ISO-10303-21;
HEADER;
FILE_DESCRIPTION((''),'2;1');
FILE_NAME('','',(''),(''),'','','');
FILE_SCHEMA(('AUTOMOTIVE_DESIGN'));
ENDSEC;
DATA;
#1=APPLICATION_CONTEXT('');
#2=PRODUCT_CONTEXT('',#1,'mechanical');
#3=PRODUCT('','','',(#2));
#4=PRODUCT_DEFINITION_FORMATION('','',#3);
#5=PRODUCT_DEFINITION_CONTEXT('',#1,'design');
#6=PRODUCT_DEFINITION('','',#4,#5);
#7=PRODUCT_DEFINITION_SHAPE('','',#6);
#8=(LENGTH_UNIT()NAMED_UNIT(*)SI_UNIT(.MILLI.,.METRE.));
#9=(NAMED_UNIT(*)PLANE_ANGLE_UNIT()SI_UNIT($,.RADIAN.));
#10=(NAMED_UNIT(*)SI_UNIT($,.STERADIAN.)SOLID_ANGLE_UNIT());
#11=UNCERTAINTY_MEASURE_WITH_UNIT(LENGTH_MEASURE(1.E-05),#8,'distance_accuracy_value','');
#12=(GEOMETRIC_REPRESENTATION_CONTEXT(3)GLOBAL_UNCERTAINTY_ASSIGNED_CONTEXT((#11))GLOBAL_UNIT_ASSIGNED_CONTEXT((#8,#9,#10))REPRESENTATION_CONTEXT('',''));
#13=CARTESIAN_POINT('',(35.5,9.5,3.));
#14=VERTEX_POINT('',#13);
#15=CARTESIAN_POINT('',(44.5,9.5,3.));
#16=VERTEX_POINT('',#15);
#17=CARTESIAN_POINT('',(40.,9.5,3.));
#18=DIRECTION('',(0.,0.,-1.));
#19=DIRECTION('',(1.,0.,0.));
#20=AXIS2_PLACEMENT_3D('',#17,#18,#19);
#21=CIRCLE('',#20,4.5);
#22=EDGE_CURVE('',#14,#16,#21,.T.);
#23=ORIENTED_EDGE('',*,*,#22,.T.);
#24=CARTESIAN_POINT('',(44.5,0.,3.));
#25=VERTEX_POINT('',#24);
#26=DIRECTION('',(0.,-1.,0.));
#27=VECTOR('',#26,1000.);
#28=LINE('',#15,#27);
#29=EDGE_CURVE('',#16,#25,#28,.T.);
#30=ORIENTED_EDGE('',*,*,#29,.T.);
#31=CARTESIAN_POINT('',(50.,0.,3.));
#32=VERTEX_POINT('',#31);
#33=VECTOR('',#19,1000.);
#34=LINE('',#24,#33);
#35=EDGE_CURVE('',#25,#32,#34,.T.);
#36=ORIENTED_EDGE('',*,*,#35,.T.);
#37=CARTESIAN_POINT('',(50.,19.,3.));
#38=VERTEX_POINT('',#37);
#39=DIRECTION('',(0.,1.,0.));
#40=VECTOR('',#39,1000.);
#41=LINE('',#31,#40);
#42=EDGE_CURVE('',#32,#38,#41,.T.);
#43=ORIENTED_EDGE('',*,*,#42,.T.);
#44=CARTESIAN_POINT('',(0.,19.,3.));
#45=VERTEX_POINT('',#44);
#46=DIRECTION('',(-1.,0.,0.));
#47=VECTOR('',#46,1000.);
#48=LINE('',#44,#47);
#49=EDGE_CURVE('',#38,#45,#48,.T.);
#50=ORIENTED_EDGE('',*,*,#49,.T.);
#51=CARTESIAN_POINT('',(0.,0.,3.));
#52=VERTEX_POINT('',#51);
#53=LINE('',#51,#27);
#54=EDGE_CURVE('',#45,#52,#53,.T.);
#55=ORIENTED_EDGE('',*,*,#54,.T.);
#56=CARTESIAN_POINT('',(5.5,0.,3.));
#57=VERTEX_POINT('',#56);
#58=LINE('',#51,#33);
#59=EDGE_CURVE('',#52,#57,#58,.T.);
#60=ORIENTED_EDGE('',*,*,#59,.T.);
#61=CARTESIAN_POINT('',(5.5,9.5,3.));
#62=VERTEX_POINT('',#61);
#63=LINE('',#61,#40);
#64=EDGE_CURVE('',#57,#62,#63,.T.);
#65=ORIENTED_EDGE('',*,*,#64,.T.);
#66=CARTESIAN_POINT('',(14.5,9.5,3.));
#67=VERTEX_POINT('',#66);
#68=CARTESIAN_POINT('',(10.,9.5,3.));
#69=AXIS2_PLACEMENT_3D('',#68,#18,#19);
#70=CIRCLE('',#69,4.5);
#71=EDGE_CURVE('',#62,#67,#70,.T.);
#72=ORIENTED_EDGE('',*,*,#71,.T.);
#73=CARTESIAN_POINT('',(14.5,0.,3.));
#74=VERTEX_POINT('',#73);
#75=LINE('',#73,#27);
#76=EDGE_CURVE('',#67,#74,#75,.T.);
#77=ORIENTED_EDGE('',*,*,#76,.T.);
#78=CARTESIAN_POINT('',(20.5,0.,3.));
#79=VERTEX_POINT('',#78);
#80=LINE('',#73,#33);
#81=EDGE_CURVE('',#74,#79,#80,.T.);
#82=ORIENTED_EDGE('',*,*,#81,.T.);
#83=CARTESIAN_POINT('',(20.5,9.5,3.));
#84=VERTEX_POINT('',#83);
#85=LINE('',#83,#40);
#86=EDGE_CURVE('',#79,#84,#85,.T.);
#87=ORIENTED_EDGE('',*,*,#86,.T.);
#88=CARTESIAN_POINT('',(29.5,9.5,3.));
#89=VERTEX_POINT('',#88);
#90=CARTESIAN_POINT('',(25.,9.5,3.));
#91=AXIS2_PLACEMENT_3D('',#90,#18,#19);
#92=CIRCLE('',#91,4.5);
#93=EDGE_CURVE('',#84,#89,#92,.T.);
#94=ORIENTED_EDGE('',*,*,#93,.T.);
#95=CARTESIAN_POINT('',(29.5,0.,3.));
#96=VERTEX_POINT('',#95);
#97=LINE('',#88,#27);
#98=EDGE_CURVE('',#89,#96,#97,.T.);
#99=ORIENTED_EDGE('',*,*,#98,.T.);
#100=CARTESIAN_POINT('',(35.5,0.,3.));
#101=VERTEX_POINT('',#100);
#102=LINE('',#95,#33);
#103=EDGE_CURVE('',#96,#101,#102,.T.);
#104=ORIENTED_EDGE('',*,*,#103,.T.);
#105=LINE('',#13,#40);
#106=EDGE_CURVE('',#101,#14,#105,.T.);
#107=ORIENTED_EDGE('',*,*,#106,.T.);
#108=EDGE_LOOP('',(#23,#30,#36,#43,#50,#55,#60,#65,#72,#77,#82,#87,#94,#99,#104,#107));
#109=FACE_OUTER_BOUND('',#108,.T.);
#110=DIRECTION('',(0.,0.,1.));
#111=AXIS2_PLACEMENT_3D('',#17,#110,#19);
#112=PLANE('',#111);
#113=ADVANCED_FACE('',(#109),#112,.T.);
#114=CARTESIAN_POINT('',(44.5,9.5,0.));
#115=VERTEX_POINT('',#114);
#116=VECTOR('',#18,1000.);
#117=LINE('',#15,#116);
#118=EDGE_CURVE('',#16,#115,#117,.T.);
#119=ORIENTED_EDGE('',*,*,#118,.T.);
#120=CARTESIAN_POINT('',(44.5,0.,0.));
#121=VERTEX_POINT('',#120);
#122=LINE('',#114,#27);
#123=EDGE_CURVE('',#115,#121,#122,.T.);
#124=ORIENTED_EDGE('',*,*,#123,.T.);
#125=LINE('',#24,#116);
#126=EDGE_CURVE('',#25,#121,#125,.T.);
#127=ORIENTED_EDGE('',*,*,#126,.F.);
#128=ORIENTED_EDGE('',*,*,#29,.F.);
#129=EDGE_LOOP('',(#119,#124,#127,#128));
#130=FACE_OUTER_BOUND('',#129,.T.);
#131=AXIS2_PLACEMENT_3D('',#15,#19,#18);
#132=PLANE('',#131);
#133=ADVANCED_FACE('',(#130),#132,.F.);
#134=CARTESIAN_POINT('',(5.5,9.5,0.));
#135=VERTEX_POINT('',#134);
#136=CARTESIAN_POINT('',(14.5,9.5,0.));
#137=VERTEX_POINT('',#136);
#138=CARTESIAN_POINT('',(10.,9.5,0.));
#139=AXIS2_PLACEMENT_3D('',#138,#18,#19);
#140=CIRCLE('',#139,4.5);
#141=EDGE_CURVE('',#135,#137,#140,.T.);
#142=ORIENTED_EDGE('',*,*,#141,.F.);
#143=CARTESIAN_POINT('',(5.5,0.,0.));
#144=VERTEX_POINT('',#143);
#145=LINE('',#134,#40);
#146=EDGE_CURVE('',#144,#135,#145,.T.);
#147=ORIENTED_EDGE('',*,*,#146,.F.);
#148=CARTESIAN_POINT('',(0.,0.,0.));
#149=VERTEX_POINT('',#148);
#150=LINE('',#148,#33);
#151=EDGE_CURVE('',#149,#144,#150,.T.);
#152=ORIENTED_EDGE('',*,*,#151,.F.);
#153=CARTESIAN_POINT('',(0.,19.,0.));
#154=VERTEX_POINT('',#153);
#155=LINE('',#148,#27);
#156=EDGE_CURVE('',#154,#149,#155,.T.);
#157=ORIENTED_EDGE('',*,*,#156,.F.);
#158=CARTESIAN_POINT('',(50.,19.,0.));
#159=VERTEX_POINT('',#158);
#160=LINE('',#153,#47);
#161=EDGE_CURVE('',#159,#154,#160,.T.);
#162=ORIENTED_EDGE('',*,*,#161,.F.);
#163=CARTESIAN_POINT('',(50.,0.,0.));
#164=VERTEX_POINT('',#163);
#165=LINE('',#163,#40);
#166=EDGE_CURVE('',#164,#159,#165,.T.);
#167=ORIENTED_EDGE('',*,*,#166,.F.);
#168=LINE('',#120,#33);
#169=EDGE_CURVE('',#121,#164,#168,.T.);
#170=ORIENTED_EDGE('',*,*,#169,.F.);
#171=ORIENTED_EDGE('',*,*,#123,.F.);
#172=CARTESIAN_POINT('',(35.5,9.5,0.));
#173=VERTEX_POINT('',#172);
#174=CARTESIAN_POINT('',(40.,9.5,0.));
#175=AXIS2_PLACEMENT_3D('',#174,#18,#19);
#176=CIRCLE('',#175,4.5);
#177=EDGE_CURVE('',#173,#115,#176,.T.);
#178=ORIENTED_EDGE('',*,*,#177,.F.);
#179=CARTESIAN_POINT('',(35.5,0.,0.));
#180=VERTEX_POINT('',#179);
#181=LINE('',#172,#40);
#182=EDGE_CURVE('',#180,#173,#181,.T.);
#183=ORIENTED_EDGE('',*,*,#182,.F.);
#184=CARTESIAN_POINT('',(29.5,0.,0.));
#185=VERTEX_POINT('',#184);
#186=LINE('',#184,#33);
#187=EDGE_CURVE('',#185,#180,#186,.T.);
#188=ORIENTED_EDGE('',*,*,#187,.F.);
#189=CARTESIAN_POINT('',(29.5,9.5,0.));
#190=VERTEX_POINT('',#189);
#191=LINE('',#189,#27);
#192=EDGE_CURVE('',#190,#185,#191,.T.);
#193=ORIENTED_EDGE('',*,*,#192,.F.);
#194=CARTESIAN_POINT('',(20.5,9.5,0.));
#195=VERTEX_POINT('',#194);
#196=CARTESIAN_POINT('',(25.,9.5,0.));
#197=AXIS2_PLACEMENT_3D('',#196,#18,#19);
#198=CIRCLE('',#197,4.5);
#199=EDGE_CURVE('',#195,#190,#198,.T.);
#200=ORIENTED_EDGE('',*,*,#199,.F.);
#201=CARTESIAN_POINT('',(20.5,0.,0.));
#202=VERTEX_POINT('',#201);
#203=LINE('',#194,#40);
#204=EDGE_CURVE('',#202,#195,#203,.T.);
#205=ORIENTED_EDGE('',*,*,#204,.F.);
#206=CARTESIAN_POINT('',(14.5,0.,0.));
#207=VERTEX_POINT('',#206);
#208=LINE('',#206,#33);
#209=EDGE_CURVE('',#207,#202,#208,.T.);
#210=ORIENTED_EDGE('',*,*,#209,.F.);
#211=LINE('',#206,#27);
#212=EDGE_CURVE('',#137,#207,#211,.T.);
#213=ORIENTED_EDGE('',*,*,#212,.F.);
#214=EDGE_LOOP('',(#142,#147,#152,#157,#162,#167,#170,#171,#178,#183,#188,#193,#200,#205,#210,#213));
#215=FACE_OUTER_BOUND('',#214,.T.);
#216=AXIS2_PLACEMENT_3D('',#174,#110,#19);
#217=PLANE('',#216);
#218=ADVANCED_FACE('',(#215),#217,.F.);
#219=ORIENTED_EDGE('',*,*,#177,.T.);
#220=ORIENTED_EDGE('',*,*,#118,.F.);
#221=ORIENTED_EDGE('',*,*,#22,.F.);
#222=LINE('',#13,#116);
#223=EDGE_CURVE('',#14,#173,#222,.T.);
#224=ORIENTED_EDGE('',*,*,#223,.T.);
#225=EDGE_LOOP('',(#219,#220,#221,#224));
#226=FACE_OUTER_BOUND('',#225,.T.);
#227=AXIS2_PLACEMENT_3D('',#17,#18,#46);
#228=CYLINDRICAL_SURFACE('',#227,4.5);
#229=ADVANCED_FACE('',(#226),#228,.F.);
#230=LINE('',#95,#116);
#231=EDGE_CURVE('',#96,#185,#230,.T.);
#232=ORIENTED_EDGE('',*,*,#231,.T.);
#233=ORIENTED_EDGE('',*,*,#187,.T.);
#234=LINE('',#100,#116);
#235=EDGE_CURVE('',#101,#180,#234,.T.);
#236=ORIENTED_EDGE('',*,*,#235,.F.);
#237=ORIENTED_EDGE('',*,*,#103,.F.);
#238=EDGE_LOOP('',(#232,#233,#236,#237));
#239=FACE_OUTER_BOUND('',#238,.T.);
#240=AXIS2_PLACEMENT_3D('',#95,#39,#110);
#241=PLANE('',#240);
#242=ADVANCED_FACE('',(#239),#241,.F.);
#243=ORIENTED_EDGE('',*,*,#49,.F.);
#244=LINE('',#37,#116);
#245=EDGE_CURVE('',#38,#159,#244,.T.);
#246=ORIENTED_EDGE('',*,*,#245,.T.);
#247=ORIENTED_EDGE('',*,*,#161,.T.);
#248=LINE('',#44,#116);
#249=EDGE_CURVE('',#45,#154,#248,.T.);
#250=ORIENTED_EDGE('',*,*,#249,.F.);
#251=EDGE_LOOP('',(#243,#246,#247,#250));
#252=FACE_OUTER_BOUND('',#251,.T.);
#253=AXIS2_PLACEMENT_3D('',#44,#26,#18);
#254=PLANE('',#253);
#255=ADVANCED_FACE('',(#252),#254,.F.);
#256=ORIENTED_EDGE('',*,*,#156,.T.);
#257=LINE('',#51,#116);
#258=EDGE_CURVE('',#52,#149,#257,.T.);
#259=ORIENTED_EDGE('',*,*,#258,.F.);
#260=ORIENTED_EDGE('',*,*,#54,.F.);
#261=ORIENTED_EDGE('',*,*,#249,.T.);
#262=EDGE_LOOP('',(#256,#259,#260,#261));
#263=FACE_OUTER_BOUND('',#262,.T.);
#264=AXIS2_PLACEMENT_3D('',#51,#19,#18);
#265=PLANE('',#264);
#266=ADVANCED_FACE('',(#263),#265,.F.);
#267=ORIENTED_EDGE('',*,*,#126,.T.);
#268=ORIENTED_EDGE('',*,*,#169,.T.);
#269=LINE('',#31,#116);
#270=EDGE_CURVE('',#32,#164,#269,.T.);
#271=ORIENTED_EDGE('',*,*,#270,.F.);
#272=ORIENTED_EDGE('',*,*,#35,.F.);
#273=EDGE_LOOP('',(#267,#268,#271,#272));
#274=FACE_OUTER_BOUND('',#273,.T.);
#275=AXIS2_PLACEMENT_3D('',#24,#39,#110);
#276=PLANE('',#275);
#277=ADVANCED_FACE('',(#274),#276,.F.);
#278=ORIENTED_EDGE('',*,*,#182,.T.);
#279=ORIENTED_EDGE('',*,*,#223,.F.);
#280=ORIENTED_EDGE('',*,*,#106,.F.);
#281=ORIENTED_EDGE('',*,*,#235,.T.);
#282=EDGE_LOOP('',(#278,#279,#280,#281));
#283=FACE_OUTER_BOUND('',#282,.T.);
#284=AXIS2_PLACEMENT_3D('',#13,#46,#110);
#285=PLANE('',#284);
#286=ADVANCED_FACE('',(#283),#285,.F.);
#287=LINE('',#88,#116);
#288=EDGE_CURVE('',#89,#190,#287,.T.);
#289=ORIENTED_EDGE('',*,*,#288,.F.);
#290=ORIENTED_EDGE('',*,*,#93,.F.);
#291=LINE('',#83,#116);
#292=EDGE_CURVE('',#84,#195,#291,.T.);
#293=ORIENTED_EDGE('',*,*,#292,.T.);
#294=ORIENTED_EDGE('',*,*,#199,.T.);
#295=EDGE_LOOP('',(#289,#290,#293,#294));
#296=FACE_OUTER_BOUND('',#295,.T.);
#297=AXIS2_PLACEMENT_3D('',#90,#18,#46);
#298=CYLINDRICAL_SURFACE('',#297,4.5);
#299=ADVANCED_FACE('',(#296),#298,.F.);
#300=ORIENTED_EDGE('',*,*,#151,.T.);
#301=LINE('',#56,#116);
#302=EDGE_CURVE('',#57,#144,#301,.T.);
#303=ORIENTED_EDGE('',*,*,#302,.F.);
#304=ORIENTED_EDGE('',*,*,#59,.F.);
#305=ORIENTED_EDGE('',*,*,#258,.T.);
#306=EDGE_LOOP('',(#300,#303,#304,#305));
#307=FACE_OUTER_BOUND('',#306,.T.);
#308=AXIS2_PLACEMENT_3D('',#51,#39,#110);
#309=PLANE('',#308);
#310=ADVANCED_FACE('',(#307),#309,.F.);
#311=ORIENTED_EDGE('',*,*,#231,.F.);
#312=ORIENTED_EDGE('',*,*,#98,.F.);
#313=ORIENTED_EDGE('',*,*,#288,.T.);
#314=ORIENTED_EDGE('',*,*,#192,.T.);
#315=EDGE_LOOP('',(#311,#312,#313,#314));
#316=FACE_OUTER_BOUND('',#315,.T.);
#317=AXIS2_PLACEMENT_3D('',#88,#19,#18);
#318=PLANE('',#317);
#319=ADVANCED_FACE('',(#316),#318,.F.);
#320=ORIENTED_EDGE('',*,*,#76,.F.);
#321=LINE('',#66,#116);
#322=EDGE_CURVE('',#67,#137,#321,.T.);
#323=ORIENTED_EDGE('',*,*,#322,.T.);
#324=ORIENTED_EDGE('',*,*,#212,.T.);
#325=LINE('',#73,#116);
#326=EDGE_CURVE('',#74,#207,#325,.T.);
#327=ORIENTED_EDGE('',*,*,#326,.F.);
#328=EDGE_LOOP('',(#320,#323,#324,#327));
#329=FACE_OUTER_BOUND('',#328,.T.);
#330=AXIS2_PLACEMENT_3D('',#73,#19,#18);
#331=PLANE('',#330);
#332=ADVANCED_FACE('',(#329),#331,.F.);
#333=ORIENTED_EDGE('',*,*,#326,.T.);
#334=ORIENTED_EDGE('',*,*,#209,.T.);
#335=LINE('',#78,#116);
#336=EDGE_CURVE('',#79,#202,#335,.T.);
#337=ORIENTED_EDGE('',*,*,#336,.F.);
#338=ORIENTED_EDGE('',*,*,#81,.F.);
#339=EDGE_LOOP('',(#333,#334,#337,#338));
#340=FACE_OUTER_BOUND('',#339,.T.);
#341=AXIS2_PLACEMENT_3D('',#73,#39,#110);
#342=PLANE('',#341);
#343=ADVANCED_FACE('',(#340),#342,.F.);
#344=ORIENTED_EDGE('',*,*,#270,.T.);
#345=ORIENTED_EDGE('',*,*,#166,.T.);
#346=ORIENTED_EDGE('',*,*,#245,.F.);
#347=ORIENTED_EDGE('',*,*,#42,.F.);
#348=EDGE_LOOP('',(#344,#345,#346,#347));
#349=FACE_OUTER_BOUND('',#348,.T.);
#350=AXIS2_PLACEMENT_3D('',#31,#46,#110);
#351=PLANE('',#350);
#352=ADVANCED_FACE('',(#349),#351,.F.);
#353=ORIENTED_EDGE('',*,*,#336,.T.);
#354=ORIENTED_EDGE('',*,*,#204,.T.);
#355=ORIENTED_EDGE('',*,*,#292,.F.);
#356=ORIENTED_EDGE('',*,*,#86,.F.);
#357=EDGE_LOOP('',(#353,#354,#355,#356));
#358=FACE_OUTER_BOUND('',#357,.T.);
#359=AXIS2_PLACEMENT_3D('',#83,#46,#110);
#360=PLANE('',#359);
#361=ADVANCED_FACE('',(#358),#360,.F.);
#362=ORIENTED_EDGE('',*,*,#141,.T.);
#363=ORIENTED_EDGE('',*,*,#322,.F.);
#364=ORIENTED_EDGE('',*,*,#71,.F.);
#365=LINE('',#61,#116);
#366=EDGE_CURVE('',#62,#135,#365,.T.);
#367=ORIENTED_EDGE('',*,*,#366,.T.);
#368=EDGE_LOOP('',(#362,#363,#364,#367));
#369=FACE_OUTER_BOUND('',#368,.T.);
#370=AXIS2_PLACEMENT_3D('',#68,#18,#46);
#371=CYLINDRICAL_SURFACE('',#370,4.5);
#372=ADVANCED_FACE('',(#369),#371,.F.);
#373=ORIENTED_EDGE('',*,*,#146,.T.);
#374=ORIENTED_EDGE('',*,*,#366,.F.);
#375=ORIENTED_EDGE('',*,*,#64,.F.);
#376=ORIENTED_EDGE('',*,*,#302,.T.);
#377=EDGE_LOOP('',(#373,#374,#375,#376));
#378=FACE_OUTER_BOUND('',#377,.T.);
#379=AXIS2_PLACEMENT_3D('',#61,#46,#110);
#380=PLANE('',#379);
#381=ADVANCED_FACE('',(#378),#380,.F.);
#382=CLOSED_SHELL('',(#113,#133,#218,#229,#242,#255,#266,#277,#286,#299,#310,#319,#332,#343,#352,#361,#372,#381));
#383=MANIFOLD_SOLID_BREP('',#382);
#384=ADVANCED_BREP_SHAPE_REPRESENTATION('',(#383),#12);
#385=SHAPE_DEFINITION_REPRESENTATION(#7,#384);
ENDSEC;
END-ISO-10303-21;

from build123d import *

# Parameters (mm, degrees)
BOSS_EXTRUDE1_DEPTH = 3


with BuildPart() as part:
    # Sketch1 → Boss-Extrude1 (new body)
    with BuildSketch(Plane.XY):
        with BuildLine():
            Line((0, 0), (5.5, 0))
            Line((5.5, 0), (5.5, 9.5))
            ThreePointArc((5.5, 9.5), (10, 14), (14.5, 9.5))
            Line((14.5, 9.5), (14.5, 0))
            Line((14.5, 0), (20.5, 0))
            Line((20.5, 0), (20.5, 9.5))
            ThreePointArc((20.5, 9.5), (25, 14), (29.5, 9.5))
            Line((29.5, 9.5), (29.5, 0))
            Line((29.5, 0), (35.5, 0))
            Line((35.5, 0), (35.5, 9.5))
            ThreePointArc((35.5, 9.5), (40, 14), (44.5, 9.5))
            Line((44.5, 9.5), (44.5, 0))
            Line((44.5, 0), (50, 0))
            Line((50, 0), (50, 19))
            Line((50, 19), (0, 19))
            Line((0, 19), (0, 0))
        make_face()
    extrude(amount=BOSS_EXTRUDE1_DEPTH)


solid = part.part
